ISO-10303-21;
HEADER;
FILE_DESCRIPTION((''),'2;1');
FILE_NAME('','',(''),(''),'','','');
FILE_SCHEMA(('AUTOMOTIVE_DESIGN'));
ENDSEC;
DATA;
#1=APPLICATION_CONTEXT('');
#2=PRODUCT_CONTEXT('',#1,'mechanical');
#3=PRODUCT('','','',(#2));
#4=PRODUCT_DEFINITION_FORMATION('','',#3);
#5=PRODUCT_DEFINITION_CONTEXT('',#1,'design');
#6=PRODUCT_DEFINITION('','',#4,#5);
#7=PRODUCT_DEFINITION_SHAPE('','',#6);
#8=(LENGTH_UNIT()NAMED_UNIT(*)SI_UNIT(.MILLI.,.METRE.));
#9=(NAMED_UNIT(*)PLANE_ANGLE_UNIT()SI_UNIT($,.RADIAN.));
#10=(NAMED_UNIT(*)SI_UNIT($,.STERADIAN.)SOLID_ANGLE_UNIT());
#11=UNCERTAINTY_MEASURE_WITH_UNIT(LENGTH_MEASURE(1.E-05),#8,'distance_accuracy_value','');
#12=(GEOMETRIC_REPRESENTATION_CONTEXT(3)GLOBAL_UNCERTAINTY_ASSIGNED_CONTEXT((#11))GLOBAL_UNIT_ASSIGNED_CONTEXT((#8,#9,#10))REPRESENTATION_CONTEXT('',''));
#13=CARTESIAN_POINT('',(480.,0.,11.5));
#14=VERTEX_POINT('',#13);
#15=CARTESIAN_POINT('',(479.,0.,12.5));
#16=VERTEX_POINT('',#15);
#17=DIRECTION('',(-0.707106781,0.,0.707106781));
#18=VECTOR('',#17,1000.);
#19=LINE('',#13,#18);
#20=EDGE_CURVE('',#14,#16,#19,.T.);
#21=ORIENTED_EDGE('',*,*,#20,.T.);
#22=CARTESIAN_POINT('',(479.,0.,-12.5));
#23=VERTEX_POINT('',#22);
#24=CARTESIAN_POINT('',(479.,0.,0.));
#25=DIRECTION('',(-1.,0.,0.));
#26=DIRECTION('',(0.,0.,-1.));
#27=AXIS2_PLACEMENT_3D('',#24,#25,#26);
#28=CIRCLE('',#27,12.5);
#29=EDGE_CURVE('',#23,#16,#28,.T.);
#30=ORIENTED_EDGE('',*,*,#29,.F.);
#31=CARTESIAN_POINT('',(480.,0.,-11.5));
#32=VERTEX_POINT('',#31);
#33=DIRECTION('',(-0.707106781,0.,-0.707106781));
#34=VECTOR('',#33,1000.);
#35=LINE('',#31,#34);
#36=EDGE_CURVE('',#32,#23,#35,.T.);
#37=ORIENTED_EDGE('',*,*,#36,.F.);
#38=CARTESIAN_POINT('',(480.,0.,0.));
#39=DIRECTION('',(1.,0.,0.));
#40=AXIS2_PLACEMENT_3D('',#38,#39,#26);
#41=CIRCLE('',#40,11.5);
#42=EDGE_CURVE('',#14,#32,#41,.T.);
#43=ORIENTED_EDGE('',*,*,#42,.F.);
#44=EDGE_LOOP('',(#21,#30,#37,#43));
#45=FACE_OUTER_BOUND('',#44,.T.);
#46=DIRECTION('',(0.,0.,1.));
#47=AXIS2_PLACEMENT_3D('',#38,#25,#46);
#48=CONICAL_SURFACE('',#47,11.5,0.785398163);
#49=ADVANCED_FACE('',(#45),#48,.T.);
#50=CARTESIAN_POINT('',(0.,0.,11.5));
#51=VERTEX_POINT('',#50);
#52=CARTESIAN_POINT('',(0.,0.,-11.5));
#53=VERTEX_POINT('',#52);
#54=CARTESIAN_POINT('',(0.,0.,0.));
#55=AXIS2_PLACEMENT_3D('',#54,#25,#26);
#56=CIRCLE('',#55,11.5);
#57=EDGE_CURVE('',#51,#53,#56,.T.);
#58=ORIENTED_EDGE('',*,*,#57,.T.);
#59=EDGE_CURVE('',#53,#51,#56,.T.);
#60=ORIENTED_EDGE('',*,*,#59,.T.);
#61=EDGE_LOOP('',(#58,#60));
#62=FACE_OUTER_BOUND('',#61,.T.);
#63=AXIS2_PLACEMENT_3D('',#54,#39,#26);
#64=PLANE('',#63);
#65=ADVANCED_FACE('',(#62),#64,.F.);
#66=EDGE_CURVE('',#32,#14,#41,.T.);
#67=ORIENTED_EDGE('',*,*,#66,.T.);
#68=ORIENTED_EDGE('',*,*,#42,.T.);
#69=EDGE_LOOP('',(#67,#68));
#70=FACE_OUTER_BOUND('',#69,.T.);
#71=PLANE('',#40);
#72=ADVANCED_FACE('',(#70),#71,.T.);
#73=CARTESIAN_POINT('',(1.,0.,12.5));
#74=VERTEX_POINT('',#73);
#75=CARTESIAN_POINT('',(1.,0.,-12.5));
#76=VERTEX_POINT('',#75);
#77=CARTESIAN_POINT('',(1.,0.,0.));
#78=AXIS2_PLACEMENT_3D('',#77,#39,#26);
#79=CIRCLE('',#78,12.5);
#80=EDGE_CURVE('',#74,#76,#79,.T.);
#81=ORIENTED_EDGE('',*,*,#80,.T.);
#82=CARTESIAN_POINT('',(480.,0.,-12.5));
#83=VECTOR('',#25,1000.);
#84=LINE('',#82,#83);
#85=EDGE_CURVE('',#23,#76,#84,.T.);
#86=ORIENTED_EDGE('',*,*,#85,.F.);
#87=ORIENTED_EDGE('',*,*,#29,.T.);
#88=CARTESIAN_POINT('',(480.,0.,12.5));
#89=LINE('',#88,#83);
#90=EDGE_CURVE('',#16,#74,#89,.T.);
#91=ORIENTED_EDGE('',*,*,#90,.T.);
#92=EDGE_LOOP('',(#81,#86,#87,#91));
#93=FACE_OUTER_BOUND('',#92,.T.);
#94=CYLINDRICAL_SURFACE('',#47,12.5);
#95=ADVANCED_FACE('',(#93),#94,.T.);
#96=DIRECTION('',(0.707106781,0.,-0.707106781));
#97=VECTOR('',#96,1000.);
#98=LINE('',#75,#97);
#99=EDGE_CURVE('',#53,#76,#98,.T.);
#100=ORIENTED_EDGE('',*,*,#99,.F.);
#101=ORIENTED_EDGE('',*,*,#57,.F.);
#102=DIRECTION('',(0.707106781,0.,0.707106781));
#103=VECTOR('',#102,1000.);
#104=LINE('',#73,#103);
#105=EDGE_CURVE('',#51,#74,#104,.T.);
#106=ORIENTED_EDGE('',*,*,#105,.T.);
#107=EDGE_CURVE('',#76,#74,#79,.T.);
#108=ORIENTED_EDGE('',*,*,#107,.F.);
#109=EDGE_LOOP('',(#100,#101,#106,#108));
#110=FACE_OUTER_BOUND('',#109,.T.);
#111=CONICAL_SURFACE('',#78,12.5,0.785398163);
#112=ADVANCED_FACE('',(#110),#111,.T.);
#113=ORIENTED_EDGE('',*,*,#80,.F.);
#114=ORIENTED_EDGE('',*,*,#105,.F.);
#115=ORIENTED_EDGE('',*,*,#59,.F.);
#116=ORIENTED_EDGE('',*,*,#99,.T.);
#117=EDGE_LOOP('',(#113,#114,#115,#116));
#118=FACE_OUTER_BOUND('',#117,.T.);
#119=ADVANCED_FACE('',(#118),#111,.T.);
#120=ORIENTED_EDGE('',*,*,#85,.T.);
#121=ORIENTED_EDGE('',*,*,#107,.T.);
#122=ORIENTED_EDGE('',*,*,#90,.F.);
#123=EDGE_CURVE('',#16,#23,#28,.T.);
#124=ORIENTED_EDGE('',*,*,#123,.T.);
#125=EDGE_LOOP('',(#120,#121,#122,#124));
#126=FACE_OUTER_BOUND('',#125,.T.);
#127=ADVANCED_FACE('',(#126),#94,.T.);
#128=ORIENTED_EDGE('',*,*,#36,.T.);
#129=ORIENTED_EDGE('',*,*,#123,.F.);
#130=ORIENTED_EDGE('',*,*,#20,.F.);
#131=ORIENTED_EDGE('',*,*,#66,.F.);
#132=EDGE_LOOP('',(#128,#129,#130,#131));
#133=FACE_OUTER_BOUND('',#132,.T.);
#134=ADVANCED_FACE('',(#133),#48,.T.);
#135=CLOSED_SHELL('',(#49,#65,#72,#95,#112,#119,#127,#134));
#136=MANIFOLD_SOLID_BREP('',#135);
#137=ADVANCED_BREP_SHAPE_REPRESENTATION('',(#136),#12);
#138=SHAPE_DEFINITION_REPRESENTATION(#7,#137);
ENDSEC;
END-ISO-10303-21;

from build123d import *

# Parameters (mm, degrees)
SKETCH1_R           = 12.5
BOSS_EXTRUDE1_DEPTH = 480
CHAMFER1_SIZE       = 1


with BuildPart() as part:
    # Sketch1 → Boss-Extrude1 (new body)
    with BuildSketch(Plane(origin=(0, 0, 0), x_dir=(0, 0, -1), z_dir=(1, 0, 0))):
        Circle(SKETCH1_R)
    extrude(amount=BOSS_EXTRUDE1_DEPTH)

    # Chamfer1
    chamfer1_edges = [part.edges().sort_by_distance(p)[0] for p in [
        (0, 0, 12.5),
        (480, 0, 12.5),
    ]]
    chamfer(chamfer1_edges, length=CHAMFER1_SIZE)


solid = part.part
